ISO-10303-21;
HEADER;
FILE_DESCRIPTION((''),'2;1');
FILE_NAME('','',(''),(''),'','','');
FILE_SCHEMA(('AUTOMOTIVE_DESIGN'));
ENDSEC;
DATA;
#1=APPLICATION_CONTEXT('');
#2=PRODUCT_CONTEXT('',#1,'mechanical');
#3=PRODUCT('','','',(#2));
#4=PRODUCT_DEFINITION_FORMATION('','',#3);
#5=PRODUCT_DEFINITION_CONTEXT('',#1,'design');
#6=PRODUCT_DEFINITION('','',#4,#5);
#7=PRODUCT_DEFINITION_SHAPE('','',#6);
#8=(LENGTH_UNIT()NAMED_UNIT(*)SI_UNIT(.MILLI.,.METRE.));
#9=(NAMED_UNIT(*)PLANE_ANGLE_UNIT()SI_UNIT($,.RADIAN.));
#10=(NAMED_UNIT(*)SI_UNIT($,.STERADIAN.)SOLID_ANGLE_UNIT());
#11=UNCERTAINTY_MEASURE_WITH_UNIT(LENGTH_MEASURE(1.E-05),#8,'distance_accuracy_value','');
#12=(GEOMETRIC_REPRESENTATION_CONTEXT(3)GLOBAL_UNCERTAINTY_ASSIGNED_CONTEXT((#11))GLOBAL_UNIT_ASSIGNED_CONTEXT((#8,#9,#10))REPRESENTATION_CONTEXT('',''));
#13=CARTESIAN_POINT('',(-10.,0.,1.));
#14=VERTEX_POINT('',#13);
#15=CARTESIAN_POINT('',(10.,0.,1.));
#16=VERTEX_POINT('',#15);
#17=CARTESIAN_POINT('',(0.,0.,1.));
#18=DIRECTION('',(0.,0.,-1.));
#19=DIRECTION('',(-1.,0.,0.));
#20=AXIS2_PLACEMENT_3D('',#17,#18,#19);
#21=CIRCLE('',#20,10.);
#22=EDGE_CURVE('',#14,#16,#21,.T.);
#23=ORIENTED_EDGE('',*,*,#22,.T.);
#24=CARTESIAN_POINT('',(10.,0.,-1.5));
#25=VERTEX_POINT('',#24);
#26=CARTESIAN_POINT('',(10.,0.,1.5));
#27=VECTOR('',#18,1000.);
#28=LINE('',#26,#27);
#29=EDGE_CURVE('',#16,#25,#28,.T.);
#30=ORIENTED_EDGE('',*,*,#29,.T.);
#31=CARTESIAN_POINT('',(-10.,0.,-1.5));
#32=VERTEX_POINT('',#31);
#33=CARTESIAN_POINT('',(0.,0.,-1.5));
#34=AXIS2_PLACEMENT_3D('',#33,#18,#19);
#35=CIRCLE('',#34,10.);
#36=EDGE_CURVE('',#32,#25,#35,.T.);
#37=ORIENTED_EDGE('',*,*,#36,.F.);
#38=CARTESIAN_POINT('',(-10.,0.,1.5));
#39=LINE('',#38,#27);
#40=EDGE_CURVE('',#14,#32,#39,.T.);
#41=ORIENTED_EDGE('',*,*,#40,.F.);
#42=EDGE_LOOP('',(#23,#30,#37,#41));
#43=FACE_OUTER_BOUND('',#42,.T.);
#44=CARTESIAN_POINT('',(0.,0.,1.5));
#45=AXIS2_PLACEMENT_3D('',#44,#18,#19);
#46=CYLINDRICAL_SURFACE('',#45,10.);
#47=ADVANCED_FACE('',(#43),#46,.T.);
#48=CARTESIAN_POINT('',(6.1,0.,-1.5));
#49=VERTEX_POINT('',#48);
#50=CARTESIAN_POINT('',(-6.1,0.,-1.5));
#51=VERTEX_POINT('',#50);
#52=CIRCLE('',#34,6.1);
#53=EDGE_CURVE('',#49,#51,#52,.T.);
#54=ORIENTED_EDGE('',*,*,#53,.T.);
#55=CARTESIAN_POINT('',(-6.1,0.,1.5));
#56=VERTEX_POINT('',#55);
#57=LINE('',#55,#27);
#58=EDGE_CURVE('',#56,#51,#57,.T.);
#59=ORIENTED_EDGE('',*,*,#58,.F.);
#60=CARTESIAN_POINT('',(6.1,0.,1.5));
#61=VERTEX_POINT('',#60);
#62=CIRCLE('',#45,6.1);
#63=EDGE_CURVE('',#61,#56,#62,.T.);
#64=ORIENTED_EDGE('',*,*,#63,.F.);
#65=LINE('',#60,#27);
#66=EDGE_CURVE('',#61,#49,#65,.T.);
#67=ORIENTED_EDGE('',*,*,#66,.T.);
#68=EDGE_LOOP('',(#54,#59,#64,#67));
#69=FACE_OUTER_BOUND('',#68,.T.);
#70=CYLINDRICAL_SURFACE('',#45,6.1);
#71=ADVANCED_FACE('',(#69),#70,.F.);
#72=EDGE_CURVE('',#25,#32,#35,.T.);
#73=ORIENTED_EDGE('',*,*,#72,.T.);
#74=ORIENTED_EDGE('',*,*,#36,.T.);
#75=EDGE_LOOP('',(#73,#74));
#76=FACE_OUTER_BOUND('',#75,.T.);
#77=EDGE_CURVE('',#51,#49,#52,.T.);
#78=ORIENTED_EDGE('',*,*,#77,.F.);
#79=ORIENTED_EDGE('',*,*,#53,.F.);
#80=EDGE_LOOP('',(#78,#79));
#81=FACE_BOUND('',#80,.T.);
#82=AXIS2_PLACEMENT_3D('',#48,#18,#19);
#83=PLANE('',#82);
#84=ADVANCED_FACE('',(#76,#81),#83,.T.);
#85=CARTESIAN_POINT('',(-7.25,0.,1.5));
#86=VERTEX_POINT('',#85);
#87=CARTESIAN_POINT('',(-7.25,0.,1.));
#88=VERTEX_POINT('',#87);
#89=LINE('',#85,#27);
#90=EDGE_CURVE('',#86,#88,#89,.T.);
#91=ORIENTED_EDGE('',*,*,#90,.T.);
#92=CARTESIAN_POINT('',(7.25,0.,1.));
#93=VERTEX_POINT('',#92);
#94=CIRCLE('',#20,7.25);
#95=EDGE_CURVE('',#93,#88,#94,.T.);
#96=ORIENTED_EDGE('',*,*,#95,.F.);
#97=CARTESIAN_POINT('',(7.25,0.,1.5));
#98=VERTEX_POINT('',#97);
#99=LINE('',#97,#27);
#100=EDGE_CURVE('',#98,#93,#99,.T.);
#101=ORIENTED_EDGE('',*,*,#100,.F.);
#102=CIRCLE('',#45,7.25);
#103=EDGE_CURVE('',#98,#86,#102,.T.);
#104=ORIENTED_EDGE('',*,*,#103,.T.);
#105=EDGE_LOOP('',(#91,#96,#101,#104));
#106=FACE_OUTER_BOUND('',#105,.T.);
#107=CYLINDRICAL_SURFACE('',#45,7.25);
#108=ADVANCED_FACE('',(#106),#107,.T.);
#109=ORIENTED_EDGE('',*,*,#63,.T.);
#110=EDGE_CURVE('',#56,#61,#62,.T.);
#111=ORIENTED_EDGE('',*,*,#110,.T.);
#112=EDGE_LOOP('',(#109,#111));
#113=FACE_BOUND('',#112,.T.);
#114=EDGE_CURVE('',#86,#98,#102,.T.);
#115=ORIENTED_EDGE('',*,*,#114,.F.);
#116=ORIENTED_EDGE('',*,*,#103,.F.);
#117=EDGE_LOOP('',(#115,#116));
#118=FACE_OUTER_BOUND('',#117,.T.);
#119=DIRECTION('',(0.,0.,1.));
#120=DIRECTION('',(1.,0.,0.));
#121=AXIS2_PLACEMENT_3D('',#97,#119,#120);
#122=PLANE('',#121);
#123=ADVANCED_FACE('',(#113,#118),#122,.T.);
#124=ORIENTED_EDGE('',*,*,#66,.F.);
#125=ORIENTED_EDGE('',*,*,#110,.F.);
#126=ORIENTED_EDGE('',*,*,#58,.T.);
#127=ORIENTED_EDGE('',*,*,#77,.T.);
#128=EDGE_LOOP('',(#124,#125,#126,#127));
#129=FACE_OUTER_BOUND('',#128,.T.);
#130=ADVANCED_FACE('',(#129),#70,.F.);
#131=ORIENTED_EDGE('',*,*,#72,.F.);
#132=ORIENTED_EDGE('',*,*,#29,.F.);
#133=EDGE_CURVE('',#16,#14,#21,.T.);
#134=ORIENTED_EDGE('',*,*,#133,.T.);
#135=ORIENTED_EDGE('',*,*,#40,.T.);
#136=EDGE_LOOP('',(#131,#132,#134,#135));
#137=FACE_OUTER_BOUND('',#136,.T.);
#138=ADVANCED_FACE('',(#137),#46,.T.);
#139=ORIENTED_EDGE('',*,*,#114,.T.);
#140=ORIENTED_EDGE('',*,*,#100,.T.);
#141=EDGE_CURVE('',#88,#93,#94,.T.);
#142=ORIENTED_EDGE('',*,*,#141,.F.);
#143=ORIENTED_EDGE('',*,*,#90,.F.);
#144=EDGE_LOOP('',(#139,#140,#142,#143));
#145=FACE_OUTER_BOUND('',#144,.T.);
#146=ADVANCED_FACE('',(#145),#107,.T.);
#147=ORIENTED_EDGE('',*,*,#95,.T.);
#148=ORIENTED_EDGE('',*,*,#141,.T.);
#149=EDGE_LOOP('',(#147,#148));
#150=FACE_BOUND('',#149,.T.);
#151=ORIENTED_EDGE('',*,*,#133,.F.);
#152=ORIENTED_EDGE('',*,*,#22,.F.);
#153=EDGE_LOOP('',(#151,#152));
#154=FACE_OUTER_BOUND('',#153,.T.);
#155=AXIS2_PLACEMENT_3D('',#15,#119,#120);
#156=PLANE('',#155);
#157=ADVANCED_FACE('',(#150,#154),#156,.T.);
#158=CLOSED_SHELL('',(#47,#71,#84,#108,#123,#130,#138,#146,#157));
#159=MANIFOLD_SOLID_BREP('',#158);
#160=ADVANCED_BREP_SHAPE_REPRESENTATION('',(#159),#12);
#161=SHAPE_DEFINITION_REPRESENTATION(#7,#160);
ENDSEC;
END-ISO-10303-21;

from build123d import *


with BuildPart() as part:
    # Sketch1 → Revolve1 (revolve)
    with BuildSketch(Plane.XZ, mode=Mode.PRIVATE) as revolve1_sk:
        Polygon((6.1, 1.5), (6.1, -1.5), (10, -1.5), (10, 1), (7.25, 1), (7.25, 1.5), align=None)
    revolve(revolve1_sk.sketch.rotate(Axis((0, 0, 1.5), (0, 0, -1)), 180), axis=Axis((0, 0, 1.5), (0, 0, -1)))


solid = part.part
